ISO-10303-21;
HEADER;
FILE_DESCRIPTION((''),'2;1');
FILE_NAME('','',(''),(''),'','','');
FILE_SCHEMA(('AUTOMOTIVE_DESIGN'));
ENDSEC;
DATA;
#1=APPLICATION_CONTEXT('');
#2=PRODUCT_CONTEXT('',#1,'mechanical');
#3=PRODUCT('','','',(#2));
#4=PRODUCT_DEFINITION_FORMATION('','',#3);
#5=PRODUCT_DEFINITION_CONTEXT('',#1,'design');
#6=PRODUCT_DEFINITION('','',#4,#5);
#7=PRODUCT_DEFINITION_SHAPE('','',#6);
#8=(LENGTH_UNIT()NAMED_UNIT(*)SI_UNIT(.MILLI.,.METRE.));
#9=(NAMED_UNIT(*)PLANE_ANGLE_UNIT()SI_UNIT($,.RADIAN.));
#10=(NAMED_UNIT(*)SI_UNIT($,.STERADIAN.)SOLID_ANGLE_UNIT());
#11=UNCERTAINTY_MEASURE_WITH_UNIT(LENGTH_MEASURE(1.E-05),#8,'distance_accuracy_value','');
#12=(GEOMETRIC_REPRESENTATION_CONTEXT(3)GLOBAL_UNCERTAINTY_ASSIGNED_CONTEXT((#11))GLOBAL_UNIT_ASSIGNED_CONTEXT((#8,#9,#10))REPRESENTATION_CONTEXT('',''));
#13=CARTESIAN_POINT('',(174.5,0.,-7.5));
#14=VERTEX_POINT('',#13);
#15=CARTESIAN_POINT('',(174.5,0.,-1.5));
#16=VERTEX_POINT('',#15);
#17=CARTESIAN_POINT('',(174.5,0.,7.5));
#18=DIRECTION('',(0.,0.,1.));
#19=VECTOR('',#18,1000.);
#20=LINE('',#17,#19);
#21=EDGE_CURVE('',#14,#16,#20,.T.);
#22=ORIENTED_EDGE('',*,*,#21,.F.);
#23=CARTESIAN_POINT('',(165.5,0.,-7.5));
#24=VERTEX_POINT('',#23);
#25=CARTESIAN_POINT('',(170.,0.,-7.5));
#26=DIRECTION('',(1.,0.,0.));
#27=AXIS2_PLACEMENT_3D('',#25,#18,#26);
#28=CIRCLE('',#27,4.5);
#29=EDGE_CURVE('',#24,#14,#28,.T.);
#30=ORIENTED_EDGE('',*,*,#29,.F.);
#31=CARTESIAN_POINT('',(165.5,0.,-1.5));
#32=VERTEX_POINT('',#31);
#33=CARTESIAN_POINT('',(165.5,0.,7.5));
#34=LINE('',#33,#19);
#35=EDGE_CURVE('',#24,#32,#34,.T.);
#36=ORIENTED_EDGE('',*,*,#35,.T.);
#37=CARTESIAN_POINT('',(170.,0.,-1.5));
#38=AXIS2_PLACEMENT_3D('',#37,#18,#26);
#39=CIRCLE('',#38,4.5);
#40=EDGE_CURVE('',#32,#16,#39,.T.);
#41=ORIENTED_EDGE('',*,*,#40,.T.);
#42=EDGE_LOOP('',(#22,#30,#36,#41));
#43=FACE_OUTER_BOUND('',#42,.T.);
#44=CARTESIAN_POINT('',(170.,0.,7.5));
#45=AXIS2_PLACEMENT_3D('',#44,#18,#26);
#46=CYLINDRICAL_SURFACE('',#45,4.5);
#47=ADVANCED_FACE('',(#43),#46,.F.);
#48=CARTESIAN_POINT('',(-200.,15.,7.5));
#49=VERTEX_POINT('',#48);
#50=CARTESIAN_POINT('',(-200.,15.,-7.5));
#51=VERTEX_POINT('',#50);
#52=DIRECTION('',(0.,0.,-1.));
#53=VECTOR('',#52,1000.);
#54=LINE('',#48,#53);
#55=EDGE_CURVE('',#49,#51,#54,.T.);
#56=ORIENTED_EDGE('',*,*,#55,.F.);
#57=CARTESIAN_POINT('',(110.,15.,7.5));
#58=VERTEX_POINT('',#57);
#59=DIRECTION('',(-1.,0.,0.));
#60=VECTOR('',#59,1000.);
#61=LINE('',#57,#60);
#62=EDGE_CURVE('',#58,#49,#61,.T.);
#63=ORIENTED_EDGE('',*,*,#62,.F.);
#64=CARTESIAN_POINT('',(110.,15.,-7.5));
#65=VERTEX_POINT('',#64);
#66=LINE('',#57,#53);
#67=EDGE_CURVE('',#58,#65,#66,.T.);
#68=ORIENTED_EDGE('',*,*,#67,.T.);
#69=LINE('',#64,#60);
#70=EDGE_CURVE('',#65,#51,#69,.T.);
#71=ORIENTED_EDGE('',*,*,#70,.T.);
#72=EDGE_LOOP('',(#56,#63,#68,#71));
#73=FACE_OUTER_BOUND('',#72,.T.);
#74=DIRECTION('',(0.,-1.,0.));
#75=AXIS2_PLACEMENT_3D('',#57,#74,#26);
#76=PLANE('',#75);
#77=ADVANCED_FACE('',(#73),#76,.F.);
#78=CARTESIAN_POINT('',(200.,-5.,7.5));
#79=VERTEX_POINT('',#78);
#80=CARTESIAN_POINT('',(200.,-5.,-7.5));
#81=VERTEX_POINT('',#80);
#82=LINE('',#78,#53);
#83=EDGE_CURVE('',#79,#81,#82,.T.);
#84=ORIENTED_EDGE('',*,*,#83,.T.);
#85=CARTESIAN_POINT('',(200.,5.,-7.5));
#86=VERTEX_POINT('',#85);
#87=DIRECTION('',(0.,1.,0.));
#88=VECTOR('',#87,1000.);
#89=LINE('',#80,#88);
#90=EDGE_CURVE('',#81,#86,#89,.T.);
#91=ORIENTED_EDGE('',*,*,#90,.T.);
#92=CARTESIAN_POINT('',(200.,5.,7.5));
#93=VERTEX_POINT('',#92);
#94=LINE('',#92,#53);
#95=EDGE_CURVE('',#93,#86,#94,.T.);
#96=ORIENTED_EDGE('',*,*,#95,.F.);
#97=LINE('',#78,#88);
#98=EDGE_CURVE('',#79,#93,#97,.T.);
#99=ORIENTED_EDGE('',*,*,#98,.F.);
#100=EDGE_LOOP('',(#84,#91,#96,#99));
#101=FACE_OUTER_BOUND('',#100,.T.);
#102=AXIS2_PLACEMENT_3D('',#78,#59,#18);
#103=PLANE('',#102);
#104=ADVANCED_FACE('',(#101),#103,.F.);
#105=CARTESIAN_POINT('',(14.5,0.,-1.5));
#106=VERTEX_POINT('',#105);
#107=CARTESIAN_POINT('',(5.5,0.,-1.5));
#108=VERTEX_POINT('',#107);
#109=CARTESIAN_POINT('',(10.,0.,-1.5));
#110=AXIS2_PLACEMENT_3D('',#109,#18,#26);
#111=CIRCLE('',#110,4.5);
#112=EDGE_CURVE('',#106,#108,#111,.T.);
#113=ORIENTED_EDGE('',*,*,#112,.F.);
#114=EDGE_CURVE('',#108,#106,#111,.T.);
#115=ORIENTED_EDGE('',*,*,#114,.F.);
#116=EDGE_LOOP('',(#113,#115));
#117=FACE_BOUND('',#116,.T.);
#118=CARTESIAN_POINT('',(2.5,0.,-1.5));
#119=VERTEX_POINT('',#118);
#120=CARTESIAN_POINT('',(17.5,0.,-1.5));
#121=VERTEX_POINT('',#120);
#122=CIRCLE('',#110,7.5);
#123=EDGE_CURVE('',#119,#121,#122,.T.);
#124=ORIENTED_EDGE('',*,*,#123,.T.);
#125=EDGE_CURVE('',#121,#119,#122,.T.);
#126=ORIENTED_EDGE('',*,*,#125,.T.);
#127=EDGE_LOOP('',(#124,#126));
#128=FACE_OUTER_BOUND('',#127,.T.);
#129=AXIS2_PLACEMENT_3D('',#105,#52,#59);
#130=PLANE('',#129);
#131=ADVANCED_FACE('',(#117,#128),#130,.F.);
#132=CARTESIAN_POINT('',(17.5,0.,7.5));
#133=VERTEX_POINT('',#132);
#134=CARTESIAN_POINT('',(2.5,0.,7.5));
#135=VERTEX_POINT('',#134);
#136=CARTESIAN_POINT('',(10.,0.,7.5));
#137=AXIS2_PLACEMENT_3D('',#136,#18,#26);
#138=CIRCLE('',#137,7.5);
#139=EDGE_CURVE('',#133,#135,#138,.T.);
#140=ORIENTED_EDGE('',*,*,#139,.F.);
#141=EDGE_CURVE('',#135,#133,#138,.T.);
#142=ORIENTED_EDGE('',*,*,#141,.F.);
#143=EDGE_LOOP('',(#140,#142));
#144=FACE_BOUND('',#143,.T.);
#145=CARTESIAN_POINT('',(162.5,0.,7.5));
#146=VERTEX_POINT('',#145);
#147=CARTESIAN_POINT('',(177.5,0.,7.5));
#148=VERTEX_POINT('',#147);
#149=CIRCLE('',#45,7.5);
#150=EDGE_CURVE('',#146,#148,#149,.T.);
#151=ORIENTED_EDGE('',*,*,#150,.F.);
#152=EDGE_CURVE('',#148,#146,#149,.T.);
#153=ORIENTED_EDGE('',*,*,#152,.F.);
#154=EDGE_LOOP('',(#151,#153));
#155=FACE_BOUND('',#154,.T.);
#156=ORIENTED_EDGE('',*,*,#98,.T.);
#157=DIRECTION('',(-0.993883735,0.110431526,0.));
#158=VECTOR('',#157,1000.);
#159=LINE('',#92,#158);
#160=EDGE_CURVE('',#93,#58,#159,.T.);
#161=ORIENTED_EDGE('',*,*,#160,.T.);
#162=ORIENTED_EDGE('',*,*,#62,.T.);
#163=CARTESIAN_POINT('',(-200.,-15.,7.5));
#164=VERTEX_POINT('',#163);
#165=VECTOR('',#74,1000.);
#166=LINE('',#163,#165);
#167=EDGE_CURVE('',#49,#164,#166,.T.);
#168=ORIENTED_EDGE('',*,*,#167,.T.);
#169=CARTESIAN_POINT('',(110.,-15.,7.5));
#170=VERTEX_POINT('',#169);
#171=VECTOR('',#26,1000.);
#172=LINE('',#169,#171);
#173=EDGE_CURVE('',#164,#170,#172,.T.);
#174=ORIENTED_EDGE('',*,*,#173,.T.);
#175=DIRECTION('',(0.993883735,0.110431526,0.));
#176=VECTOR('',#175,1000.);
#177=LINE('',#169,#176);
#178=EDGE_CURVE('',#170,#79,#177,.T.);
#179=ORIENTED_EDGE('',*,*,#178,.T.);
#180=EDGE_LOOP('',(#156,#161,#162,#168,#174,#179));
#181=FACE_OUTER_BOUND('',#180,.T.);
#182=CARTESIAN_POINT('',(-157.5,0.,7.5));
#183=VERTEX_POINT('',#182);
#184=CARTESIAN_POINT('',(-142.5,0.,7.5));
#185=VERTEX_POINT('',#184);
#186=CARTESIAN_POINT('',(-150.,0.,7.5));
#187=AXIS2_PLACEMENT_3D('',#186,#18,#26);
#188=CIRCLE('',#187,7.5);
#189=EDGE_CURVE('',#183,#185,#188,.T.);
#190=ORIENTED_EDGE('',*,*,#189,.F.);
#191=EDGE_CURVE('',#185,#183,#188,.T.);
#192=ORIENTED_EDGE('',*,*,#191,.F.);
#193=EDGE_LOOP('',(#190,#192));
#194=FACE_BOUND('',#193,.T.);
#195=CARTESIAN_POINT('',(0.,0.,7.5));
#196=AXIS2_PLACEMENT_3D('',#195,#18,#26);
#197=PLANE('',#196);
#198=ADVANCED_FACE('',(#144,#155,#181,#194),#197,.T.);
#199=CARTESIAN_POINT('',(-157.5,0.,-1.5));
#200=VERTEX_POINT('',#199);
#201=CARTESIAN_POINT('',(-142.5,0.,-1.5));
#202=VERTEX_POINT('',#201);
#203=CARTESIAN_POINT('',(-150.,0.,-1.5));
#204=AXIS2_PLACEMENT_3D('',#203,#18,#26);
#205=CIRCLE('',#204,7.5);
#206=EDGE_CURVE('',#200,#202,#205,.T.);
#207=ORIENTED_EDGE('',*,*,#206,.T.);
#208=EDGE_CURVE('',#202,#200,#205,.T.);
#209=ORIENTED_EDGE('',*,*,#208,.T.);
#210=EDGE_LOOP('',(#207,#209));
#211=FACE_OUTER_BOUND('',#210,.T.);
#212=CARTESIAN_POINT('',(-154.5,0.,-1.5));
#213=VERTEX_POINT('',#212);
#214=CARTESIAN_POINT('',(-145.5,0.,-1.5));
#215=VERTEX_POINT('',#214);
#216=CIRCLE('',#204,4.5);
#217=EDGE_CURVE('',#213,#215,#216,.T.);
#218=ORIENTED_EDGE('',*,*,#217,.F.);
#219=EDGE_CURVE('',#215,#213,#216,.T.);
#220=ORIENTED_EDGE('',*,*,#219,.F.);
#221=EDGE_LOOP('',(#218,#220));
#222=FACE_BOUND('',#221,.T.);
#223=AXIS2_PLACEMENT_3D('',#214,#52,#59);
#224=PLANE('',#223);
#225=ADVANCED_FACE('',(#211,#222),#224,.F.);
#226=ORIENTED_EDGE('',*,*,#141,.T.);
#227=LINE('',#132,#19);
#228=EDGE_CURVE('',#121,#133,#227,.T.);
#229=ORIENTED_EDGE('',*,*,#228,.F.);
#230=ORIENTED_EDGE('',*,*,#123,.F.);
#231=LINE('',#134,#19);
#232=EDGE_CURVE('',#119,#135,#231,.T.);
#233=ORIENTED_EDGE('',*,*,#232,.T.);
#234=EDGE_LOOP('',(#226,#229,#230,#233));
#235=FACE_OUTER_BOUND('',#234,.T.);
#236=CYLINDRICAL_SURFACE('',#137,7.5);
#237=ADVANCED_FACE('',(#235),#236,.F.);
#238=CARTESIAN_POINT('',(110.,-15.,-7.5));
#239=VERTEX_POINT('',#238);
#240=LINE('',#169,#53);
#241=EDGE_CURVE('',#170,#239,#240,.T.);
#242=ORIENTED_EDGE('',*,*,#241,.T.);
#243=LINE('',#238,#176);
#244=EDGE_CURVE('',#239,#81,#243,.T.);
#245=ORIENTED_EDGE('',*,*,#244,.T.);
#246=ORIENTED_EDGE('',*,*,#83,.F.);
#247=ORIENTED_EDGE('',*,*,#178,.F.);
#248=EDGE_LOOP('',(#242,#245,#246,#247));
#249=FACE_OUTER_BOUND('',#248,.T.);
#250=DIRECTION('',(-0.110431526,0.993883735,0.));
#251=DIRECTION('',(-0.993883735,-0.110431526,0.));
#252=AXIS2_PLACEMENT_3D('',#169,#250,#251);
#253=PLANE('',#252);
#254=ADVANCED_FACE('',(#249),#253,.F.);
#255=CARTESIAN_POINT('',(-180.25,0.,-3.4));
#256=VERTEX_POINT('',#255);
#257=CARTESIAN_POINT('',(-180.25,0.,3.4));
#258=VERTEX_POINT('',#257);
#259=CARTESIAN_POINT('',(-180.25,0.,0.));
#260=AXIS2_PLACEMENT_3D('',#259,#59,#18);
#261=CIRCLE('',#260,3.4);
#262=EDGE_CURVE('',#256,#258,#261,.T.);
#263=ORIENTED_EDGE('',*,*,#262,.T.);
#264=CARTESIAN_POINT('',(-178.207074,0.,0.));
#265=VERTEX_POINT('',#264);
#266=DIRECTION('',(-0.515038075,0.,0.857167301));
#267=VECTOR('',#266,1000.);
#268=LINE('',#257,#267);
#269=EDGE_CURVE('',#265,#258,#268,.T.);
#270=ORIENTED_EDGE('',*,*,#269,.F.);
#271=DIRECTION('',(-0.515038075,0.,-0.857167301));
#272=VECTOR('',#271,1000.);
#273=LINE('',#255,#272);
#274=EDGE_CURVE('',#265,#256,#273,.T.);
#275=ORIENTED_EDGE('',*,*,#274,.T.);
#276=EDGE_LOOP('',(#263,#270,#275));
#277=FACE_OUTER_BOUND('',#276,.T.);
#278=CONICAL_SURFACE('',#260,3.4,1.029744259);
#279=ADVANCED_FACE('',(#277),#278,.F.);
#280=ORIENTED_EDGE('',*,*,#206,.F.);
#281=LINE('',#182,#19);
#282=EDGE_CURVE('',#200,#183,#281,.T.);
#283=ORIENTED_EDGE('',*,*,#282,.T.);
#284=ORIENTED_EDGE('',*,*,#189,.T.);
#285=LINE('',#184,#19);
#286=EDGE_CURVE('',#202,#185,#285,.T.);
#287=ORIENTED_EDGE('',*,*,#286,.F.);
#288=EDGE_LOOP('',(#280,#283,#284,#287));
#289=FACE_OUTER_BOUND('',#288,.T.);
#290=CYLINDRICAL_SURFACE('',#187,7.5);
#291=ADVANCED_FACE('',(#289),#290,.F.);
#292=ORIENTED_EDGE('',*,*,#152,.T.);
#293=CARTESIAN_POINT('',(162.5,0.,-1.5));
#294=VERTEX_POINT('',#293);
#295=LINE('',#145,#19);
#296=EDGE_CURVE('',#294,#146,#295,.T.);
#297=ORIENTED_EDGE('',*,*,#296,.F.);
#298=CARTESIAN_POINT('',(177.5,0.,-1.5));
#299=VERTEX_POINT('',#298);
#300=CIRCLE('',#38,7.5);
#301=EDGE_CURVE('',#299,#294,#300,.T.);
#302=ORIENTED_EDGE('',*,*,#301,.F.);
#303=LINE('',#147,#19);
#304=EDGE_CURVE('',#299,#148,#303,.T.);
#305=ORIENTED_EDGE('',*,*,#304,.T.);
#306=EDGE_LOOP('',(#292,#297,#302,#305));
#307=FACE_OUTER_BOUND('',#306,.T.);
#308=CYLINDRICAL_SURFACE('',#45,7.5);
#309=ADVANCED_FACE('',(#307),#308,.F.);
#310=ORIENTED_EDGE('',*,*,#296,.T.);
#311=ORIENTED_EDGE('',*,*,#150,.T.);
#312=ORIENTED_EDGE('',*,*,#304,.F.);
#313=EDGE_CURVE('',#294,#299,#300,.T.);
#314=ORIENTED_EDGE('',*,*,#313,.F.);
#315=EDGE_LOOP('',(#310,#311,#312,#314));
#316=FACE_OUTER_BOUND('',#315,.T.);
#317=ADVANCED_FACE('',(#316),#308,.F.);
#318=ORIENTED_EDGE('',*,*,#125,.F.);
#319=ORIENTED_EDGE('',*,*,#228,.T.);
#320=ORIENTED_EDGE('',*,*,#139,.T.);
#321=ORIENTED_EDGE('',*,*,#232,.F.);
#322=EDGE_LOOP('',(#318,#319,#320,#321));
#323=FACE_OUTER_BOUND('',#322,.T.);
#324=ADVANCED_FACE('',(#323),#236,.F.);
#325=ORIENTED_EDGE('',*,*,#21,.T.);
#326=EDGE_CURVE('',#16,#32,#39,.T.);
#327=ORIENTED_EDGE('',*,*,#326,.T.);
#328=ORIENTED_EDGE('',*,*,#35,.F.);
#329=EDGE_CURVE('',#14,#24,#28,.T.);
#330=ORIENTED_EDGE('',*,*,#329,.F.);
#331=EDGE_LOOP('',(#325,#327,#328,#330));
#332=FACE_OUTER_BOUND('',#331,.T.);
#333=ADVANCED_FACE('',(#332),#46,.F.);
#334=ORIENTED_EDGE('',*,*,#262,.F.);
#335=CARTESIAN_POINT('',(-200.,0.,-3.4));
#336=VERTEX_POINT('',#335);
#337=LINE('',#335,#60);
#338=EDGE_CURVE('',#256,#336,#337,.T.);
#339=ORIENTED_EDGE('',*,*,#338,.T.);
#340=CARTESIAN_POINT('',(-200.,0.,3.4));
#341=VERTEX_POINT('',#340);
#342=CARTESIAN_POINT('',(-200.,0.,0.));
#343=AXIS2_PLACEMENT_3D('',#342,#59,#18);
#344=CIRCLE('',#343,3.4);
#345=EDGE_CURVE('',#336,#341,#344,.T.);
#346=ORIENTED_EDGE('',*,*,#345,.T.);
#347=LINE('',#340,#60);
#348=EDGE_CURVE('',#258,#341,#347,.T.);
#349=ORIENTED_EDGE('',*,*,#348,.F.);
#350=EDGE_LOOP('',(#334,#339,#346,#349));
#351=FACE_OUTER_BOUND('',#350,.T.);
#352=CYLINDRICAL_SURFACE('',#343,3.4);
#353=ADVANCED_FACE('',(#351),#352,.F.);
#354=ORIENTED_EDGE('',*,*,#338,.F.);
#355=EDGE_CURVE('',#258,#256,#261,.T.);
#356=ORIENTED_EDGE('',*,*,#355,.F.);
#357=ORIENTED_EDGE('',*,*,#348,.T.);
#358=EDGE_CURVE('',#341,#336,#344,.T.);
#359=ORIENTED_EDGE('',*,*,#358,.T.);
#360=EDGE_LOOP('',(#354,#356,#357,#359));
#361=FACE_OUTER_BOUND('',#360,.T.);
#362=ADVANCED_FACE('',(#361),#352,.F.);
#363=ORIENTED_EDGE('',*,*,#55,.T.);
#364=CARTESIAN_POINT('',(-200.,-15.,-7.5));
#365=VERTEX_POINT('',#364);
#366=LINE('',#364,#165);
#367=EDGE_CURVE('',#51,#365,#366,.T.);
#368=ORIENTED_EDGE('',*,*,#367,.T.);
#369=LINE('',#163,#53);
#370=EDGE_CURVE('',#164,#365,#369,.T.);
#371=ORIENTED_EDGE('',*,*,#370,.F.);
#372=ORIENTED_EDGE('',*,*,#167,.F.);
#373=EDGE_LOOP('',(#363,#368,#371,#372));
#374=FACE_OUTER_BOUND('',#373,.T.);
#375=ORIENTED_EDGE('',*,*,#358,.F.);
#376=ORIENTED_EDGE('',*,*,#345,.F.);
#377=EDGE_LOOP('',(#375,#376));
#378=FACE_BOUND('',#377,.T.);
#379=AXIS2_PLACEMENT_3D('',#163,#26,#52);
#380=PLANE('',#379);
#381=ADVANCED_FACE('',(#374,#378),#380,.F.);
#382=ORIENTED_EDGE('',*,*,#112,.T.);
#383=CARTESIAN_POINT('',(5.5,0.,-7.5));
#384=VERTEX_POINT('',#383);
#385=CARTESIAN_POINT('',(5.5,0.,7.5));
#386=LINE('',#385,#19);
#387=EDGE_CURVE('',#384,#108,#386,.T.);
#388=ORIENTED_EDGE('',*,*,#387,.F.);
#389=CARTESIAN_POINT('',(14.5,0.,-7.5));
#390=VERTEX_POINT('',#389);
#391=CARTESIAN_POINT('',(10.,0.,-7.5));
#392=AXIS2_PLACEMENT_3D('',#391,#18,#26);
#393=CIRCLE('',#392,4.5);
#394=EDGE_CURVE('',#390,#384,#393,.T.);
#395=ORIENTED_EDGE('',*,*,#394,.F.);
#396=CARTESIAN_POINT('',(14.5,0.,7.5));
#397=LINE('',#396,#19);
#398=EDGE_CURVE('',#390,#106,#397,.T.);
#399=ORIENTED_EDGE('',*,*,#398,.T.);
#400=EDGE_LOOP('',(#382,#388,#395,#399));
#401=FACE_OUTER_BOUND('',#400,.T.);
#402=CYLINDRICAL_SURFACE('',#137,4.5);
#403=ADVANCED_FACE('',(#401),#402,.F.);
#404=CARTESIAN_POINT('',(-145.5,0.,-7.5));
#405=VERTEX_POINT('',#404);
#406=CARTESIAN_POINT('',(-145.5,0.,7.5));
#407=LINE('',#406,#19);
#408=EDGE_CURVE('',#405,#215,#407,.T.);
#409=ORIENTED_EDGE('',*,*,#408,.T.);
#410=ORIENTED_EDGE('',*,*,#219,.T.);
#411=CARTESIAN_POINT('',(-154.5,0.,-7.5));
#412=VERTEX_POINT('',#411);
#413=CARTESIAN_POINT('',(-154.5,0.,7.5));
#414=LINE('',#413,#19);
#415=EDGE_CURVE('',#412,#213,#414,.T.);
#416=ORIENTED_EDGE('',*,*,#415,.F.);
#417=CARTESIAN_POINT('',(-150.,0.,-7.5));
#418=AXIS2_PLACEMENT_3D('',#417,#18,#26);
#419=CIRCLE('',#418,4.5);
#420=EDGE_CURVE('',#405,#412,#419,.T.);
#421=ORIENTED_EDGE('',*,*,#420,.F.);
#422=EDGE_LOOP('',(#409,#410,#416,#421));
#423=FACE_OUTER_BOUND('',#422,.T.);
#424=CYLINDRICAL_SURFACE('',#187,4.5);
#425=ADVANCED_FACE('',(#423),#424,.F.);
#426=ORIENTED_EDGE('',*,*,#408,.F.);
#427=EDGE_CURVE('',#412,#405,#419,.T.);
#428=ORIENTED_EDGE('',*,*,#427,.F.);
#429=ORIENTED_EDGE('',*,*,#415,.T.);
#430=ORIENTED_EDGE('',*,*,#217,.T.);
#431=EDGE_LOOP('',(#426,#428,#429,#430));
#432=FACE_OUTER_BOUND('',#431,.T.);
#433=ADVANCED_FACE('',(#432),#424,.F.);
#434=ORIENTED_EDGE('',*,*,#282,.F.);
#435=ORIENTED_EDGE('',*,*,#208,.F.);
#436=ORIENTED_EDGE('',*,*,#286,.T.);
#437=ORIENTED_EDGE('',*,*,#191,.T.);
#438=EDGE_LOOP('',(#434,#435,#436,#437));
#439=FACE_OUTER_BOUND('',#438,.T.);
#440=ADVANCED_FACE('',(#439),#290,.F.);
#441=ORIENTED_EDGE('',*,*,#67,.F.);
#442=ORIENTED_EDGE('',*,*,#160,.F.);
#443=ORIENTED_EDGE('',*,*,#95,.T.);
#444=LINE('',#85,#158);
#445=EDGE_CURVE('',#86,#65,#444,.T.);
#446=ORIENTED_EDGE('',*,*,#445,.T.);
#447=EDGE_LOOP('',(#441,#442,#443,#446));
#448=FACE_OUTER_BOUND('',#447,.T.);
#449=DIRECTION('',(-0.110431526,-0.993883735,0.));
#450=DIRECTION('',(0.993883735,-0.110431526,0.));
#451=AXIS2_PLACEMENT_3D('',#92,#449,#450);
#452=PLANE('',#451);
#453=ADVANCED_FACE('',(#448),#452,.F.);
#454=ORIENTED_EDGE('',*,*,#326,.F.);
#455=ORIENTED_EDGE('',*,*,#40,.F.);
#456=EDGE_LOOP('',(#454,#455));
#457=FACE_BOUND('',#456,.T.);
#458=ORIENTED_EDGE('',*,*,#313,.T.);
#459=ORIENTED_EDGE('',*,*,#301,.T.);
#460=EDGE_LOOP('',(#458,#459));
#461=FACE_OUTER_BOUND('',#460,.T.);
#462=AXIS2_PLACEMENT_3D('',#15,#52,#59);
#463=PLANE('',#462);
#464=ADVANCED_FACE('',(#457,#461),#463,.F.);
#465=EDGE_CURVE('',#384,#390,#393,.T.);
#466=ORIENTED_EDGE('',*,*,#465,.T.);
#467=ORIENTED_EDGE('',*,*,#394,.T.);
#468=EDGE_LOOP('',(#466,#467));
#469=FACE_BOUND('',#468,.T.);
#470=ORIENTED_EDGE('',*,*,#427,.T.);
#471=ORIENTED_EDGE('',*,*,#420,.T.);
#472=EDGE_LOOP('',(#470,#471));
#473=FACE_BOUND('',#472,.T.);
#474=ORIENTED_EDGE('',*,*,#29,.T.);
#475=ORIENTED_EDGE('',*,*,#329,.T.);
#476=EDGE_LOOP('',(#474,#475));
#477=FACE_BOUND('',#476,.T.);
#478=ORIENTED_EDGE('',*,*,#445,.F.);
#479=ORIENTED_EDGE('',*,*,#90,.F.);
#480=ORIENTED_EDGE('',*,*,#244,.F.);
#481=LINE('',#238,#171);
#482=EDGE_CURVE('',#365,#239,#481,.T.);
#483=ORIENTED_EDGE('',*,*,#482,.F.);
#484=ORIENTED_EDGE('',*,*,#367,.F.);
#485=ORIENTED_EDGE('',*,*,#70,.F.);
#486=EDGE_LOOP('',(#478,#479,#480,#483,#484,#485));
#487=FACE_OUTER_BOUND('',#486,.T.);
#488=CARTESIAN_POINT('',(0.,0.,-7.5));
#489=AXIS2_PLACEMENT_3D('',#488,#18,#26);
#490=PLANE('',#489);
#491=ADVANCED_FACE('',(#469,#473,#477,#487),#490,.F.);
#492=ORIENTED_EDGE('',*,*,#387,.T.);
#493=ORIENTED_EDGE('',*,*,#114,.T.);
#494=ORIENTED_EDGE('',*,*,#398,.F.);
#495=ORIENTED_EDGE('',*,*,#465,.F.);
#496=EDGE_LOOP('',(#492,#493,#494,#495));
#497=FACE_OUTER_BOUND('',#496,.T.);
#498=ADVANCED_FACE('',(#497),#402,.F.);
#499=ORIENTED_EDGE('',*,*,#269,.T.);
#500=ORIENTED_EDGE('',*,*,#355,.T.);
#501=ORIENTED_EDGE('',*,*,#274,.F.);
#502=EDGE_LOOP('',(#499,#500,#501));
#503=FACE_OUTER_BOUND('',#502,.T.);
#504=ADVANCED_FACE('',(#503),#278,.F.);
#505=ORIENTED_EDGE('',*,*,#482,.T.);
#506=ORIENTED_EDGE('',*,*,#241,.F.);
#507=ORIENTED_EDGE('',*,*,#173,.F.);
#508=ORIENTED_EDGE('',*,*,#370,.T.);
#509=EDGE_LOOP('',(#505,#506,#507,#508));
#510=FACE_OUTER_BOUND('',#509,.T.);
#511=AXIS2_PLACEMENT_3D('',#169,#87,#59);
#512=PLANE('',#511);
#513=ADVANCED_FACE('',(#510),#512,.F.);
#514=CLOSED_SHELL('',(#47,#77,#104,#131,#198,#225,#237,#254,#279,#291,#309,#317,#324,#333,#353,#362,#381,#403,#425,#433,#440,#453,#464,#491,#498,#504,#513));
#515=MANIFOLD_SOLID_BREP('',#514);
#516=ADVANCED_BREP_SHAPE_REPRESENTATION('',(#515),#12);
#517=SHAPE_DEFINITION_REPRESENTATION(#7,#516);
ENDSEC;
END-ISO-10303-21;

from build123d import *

# Parameters (mm, degrees)
EXTRUDE_1_DEPTH           = 7.5
HOLE_WIZARD_M8_1_D        = 6.8
HOLE_WIZARD_M8_1_DEPTH    = 19.75
HOLE_WIZARD_M8_1_TIP      = 2.042926105
HOLE_WIZARD_1_D           = 9
HOLE_WIZARD_1_CBORE_D     = 15
HOLE_WIZARD_1_CBORE_DEPTH = 9


with BuildPart() as part:
    # 草图1 → 凸台-拉伸1 (new, symmetric)
    with BuildSketch(Plane.XY):
        Polygon((200, 5), (110, 15), (-200, 15), (-200, -15), (110, -15), (200, -5), align=None)
    extrude(amount=EXTRUDE_1_DEPTH, both=True)

    # M8 螺纹孔1
    with Locations(Plane(origin=(-200, 0, 0), x_dir=(0, 0, -1), z_dir=(-1, 0, 0))):
        with Locations((0, 0)):
            Hole(HOLE_WIZARD_M8_1_D / 2, depth=HOLE_WIZARD_M8_1_DEPTH)
            with Locations((0, 0, -(HOLE_WIZARD_M8_1_DEPTH + HOLE_WIZARD_M8_1_TIP / 2))):  # 118° drill point
                Cone(0, HOLE_WIZARD_M8_1_D / 2, HOLE_WIZARD_M8_1_TIP, mode=Mode.SUBTRACT)

    # 打孔尺寸(%根据)内六角圆柱头螺钉的类型1 (through all)
    with Locations(Plane(origin=(-150, 0, 7.5), x_dir=(1, 0, 0), z_dir=(0, 0, 1))):
        with Locations((0, 0), (320, 0), (160, 0)):
            CounterBoreHole(HOLE_WIZARD_1_D / 2, HOLE_WIZARD_1_CBORE_D / 2, HOLE_WIZARD_1_CBORE_DEPTH)


solid = part.part
